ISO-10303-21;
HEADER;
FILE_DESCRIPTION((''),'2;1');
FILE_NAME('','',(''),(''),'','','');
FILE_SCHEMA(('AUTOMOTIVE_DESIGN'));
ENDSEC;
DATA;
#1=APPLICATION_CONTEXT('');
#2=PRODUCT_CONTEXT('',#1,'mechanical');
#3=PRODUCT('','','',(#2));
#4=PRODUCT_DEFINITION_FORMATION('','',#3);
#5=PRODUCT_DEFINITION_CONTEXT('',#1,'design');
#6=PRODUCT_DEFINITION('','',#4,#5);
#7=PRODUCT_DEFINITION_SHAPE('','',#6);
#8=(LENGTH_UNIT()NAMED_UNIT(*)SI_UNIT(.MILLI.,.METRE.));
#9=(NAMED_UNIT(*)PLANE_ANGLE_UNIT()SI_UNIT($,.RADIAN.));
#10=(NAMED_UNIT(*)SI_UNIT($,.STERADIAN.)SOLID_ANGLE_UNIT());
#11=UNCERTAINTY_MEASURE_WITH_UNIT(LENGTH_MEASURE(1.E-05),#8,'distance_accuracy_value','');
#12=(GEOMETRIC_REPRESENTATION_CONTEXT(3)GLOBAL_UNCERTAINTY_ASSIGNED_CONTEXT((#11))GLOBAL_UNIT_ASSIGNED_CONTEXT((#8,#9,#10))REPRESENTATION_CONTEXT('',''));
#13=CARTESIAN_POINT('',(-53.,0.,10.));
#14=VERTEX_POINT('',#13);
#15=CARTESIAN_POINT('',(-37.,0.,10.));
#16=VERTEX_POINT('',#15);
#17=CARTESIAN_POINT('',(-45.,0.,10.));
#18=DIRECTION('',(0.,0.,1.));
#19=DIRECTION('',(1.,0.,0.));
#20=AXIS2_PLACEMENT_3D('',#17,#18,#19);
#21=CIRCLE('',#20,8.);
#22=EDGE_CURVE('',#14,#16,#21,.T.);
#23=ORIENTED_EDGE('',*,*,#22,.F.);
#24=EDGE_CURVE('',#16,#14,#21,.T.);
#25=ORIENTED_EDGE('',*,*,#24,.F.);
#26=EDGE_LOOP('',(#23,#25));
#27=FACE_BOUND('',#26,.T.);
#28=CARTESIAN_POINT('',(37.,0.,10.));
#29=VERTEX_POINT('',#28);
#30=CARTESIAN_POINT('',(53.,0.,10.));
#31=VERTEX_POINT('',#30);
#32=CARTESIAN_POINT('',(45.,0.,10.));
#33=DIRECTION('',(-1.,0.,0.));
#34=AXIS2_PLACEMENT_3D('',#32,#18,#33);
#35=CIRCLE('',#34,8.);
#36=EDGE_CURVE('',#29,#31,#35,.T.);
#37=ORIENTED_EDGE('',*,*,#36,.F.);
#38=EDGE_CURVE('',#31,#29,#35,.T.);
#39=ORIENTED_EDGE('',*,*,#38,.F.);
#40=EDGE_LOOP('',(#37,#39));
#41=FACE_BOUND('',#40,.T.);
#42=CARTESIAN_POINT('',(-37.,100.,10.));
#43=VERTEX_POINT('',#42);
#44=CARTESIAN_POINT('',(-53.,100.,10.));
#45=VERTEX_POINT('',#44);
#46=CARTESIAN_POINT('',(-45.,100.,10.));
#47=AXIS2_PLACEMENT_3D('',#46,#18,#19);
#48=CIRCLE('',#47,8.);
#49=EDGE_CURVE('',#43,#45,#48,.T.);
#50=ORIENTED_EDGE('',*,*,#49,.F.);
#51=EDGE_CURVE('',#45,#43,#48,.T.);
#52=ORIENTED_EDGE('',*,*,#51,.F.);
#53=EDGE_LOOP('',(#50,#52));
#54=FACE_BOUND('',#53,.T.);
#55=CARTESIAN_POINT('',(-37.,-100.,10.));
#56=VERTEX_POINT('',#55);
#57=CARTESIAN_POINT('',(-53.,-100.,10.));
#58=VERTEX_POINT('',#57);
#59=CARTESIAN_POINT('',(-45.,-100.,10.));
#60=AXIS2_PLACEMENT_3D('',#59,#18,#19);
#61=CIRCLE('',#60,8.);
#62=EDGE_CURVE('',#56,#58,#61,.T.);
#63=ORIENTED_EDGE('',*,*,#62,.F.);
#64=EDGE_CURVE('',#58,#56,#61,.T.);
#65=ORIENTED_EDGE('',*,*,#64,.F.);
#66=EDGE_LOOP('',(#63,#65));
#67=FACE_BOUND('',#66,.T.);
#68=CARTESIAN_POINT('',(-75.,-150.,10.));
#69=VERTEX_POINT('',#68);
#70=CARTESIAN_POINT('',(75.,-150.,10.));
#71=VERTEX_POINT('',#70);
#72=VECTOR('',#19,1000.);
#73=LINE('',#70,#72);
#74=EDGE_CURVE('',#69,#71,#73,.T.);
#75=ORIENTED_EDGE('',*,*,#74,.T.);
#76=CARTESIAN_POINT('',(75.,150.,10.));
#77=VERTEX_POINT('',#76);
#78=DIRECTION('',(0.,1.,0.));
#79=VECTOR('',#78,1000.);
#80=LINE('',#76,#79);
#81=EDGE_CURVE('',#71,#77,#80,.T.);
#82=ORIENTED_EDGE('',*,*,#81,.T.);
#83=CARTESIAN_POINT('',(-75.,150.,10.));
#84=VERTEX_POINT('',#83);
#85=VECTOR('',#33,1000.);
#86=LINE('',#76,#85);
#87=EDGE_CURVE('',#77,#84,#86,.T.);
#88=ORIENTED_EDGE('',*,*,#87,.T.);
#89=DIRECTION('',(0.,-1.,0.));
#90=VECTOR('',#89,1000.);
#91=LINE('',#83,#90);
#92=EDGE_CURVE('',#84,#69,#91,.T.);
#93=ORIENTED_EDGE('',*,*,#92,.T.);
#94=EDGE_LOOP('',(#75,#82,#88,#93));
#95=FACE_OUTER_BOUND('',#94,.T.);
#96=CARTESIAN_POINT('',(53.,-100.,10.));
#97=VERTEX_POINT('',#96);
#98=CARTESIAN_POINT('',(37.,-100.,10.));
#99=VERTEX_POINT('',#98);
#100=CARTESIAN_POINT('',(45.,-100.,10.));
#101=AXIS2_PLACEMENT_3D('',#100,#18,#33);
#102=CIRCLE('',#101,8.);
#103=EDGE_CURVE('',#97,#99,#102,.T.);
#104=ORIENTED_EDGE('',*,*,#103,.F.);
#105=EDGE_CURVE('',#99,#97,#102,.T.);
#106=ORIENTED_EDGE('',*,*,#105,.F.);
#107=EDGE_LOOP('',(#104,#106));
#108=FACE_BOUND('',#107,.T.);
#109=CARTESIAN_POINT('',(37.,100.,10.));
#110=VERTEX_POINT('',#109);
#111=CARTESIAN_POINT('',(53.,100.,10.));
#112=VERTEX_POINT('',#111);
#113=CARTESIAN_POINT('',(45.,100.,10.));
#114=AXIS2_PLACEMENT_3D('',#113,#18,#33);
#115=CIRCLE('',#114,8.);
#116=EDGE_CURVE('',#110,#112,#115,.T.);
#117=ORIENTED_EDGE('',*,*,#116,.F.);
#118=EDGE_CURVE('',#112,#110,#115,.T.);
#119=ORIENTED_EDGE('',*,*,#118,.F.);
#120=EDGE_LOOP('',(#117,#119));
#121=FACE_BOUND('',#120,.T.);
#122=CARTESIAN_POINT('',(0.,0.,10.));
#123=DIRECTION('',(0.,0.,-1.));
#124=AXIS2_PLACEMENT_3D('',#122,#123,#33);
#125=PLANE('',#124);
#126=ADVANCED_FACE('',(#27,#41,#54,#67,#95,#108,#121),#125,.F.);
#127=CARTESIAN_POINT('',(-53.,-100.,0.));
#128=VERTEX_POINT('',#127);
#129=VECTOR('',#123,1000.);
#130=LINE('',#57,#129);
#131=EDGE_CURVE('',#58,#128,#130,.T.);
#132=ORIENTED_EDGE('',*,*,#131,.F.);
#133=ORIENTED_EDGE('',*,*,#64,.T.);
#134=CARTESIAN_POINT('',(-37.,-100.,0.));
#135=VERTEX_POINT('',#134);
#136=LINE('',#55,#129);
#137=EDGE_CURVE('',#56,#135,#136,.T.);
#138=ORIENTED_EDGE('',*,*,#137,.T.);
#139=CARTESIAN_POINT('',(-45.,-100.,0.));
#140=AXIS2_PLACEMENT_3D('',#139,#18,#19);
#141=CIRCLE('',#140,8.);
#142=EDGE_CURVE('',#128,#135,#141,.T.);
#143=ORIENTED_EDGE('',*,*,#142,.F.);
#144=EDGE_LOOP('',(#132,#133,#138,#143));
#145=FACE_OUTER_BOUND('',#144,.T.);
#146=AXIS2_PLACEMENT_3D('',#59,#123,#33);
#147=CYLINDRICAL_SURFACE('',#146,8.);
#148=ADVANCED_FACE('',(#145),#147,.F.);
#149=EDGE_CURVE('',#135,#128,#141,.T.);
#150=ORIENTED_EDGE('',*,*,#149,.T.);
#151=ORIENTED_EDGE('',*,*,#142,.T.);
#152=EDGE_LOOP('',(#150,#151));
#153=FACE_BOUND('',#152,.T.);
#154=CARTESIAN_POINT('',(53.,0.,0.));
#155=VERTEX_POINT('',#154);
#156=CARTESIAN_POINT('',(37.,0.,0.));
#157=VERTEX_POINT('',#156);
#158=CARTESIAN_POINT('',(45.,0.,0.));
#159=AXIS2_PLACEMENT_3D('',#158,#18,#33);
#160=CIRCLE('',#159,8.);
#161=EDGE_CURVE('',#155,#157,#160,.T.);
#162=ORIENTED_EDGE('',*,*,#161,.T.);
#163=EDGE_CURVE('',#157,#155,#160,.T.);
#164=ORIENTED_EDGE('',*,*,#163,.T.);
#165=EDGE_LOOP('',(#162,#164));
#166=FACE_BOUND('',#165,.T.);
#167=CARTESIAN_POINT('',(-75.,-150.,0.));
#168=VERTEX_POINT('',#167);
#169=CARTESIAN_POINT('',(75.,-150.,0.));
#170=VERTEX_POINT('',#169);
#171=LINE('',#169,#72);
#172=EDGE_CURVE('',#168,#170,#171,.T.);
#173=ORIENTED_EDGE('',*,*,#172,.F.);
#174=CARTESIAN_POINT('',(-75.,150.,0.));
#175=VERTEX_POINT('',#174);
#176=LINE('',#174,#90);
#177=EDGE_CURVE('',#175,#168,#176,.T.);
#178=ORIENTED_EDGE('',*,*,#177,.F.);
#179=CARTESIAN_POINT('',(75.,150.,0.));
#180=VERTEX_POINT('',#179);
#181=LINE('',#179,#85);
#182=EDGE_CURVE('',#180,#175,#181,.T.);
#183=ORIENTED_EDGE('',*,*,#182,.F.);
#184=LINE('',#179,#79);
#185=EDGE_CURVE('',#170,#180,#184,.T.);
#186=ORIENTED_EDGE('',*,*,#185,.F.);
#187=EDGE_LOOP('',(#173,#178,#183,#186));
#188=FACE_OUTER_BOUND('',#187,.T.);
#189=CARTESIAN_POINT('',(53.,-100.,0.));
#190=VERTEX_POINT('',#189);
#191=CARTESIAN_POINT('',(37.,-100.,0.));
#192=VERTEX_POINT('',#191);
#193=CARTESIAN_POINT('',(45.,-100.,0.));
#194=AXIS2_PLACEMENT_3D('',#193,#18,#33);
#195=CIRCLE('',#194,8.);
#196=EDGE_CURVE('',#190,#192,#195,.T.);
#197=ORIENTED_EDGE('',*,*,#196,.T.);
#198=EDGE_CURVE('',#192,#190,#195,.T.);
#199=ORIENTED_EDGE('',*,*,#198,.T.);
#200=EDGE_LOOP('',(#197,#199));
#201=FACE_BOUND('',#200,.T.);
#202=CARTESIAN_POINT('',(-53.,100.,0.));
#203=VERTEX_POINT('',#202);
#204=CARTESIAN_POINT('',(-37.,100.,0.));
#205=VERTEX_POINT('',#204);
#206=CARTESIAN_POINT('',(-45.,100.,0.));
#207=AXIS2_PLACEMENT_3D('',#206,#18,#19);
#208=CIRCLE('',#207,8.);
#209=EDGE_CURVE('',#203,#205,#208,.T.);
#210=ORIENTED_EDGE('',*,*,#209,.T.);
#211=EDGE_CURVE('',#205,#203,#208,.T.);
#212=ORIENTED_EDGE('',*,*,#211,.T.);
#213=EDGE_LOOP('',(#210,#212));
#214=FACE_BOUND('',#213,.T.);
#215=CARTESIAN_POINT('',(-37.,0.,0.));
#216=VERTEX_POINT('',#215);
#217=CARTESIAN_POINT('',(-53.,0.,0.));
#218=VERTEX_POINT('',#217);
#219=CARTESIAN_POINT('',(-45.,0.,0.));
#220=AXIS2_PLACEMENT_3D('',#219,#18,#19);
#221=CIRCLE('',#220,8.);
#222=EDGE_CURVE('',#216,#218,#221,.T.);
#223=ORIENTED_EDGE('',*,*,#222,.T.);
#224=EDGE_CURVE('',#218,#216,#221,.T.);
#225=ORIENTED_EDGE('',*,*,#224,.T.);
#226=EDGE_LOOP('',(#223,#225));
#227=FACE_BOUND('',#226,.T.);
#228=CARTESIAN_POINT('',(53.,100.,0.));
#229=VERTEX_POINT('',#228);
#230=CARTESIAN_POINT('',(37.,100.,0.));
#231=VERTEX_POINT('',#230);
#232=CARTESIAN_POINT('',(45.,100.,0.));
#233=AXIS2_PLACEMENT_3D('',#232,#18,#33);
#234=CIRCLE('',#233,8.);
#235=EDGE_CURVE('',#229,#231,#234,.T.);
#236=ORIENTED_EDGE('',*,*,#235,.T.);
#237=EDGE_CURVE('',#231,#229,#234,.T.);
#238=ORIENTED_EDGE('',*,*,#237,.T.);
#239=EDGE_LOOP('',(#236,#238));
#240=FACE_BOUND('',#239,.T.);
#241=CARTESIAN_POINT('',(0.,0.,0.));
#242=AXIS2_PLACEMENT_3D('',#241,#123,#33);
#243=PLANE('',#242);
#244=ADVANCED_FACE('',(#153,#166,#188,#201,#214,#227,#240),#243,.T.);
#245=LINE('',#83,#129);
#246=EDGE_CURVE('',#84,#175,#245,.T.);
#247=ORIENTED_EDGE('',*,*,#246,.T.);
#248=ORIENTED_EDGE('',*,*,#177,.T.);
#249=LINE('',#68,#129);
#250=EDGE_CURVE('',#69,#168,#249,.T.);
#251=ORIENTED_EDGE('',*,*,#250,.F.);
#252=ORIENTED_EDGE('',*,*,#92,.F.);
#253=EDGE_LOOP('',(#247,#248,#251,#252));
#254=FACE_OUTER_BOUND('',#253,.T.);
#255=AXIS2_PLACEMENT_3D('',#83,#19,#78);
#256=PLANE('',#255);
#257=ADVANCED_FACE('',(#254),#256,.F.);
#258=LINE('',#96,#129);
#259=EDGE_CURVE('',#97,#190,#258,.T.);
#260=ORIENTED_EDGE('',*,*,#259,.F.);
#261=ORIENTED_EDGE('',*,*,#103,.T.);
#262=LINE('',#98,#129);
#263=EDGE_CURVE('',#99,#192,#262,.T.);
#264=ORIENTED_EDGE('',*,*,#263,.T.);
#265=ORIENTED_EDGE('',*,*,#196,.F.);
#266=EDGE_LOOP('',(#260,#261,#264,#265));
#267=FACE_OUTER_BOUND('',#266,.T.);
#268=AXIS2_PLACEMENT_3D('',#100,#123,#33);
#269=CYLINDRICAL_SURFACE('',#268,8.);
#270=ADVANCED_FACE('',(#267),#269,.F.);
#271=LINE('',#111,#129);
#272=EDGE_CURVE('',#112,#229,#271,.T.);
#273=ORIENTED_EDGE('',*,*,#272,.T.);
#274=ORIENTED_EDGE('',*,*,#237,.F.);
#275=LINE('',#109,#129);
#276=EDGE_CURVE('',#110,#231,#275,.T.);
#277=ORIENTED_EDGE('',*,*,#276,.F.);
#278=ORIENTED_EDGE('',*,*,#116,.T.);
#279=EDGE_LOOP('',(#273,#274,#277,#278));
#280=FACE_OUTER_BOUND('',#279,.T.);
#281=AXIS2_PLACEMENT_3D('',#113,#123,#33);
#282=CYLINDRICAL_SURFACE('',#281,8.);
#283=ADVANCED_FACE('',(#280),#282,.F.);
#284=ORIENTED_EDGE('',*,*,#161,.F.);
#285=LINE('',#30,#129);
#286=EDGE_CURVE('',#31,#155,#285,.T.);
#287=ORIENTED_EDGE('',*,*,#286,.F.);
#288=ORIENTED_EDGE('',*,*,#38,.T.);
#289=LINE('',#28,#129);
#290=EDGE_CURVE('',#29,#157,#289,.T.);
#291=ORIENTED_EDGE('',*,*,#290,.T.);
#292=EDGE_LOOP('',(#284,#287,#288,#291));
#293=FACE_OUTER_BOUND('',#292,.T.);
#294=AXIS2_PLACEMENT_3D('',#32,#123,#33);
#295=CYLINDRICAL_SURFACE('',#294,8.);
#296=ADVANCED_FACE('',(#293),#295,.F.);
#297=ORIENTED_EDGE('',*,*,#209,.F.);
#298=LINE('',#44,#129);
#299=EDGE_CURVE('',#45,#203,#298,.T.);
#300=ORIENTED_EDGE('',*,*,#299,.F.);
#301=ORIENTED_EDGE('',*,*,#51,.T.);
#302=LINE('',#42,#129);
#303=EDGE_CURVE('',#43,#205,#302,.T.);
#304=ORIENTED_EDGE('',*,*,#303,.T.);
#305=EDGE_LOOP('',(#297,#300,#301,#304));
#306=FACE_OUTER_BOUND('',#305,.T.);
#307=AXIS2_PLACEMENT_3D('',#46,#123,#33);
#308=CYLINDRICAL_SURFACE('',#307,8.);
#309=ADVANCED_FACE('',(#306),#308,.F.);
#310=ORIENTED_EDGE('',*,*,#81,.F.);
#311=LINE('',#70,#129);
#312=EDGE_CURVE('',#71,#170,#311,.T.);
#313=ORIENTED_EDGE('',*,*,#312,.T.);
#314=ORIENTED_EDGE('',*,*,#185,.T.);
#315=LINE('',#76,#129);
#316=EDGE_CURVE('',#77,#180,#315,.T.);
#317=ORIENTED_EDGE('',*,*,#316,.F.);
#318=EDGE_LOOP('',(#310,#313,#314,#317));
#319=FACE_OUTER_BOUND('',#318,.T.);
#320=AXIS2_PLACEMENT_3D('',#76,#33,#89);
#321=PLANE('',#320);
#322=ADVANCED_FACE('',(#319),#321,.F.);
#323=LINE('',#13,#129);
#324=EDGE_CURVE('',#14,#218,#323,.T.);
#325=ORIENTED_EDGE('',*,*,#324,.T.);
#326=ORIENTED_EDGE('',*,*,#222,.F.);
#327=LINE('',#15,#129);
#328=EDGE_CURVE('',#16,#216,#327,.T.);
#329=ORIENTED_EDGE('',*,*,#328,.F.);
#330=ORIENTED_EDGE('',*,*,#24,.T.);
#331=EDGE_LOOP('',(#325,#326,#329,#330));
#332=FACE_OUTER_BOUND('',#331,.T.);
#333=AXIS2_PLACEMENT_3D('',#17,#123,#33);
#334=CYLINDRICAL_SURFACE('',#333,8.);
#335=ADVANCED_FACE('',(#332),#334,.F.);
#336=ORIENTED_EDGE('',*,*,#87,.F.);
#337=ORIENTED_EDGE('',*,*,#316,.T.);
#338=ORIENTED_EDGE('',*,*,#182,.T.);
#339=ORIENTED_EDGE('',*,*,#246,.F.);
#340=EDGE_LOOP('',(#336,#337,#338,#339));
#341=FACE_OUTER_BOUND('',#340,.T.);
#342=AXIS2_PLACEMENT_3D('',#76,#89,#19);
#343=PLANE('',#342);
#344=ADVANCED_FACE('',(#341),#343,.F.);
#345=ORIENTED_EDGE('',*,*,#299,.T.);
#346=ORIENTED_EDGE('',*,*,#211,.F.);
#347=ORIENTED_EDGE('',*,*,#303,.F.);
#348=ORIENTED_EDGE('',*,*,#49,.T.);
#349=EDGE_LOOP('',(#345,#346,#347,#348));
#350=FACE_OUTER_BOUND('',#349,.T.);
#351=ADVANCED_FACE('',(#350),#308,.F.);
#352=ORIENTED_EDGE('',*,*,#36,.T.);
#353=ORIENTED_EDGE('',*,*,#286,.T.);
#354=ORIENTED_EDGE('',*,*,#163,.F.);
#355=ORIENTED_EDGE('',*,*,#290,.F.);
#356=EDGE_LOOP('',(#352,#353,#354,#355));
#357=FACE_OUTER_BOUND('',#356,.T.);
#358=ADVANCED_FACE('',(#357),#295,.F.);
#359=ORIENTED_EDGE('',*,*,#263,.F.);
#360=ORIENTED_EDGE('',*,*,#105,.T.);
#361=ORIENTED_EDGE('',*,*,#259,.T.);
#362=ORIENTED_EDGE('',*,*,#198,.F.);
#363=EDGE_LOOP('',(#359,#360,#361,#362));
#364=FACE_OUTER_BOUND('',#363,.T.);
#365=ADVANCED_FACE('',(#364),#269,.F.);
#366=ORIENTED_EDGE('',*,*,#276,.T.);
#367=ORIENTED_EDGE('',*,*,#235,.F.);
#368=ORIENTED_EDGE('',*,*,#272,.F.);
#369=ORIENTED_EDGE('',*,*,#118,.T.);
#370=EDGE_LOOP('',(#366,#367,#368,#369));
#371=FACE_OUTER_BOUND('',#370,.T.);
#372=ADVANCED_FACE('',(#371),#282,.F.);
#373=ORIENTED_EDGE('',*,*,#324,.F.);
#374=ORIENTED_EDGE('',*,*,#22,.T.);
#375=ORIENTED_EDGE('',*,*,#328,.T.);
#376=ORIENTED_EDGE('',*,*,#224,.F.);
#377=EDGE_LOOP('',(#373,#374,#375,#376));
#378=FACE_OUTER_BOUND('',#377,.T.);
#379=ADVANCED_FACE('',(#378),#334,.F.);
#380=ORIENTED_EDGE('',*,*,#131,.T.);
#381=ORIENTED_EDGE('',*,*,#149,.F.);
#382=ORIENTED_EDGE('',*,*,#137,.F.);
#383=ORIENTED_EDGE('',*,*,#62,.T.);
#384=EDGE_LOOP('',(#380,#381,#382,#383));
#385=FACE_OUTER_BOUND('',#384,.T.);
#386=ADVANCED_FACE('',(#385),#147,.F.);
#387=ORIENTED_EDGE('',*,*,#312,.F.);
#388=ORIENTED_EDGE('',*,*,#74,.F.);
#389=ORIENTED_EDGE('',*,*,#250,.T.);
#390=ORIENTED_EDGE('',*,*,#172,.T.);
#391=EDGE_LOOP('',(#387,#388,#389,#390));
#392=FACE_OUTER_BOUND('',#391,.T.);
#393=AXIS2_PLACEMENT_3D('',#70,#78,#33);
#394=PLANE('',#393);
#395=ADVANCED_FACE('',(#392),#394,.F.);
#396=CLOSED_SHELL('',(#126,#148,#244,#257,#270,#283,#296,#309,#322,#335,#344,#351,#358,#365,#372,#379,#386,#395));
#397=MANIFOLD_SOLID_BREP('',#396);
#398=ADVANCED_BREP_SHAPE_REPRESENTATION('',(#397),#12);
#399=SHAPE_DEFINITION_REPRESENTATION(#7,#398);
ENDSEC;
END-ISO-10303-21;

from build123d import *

# Parameters (mm, degrees)
SKETCH1_W           = 150
SKETCH1_H           = 300
SKETCH1_R           = 8
BOSS_EXTRUDE1_DEPTH = 10


with BuildPart() as part:
    # Sketch1 → Boss-Extrude1 (new body)
    with BuildSketch(Plane.XY):
        Rectangle(SKETCH1_W, SKETCH1_H)
        with Locations((-45, 100)):
            Circle(SKETCH1_R, mode=Mode.SUBTRACT)
        with Locations((-45, 0)):
            Circle(SKETCH1_R, mode=Mode.SUBTRACT)
        with Locations((-45, -100)):
            Circle(SKETCH1_R, mode=Mode.SUBTRACT)
        with Locations(Location((45, -100, 0), (0, 0, 180))):
            Circle(SKETCH1_R, mode=Mode.SUBTRACT)
        with Locations(Location((45, 0, 0), (0, 0, 180))):
            Circle(SKETCH1_R, mode=Mode.SUBTRACT)
        with Locations(Location((45, 100, 0), (0, 0, 180))):
            Circle(SKETCH1_R, mode=Mode.SUBTRACT)
    extrude(amount=BOSS_EXTRUDE1_DEPTH)


solid = part.part
